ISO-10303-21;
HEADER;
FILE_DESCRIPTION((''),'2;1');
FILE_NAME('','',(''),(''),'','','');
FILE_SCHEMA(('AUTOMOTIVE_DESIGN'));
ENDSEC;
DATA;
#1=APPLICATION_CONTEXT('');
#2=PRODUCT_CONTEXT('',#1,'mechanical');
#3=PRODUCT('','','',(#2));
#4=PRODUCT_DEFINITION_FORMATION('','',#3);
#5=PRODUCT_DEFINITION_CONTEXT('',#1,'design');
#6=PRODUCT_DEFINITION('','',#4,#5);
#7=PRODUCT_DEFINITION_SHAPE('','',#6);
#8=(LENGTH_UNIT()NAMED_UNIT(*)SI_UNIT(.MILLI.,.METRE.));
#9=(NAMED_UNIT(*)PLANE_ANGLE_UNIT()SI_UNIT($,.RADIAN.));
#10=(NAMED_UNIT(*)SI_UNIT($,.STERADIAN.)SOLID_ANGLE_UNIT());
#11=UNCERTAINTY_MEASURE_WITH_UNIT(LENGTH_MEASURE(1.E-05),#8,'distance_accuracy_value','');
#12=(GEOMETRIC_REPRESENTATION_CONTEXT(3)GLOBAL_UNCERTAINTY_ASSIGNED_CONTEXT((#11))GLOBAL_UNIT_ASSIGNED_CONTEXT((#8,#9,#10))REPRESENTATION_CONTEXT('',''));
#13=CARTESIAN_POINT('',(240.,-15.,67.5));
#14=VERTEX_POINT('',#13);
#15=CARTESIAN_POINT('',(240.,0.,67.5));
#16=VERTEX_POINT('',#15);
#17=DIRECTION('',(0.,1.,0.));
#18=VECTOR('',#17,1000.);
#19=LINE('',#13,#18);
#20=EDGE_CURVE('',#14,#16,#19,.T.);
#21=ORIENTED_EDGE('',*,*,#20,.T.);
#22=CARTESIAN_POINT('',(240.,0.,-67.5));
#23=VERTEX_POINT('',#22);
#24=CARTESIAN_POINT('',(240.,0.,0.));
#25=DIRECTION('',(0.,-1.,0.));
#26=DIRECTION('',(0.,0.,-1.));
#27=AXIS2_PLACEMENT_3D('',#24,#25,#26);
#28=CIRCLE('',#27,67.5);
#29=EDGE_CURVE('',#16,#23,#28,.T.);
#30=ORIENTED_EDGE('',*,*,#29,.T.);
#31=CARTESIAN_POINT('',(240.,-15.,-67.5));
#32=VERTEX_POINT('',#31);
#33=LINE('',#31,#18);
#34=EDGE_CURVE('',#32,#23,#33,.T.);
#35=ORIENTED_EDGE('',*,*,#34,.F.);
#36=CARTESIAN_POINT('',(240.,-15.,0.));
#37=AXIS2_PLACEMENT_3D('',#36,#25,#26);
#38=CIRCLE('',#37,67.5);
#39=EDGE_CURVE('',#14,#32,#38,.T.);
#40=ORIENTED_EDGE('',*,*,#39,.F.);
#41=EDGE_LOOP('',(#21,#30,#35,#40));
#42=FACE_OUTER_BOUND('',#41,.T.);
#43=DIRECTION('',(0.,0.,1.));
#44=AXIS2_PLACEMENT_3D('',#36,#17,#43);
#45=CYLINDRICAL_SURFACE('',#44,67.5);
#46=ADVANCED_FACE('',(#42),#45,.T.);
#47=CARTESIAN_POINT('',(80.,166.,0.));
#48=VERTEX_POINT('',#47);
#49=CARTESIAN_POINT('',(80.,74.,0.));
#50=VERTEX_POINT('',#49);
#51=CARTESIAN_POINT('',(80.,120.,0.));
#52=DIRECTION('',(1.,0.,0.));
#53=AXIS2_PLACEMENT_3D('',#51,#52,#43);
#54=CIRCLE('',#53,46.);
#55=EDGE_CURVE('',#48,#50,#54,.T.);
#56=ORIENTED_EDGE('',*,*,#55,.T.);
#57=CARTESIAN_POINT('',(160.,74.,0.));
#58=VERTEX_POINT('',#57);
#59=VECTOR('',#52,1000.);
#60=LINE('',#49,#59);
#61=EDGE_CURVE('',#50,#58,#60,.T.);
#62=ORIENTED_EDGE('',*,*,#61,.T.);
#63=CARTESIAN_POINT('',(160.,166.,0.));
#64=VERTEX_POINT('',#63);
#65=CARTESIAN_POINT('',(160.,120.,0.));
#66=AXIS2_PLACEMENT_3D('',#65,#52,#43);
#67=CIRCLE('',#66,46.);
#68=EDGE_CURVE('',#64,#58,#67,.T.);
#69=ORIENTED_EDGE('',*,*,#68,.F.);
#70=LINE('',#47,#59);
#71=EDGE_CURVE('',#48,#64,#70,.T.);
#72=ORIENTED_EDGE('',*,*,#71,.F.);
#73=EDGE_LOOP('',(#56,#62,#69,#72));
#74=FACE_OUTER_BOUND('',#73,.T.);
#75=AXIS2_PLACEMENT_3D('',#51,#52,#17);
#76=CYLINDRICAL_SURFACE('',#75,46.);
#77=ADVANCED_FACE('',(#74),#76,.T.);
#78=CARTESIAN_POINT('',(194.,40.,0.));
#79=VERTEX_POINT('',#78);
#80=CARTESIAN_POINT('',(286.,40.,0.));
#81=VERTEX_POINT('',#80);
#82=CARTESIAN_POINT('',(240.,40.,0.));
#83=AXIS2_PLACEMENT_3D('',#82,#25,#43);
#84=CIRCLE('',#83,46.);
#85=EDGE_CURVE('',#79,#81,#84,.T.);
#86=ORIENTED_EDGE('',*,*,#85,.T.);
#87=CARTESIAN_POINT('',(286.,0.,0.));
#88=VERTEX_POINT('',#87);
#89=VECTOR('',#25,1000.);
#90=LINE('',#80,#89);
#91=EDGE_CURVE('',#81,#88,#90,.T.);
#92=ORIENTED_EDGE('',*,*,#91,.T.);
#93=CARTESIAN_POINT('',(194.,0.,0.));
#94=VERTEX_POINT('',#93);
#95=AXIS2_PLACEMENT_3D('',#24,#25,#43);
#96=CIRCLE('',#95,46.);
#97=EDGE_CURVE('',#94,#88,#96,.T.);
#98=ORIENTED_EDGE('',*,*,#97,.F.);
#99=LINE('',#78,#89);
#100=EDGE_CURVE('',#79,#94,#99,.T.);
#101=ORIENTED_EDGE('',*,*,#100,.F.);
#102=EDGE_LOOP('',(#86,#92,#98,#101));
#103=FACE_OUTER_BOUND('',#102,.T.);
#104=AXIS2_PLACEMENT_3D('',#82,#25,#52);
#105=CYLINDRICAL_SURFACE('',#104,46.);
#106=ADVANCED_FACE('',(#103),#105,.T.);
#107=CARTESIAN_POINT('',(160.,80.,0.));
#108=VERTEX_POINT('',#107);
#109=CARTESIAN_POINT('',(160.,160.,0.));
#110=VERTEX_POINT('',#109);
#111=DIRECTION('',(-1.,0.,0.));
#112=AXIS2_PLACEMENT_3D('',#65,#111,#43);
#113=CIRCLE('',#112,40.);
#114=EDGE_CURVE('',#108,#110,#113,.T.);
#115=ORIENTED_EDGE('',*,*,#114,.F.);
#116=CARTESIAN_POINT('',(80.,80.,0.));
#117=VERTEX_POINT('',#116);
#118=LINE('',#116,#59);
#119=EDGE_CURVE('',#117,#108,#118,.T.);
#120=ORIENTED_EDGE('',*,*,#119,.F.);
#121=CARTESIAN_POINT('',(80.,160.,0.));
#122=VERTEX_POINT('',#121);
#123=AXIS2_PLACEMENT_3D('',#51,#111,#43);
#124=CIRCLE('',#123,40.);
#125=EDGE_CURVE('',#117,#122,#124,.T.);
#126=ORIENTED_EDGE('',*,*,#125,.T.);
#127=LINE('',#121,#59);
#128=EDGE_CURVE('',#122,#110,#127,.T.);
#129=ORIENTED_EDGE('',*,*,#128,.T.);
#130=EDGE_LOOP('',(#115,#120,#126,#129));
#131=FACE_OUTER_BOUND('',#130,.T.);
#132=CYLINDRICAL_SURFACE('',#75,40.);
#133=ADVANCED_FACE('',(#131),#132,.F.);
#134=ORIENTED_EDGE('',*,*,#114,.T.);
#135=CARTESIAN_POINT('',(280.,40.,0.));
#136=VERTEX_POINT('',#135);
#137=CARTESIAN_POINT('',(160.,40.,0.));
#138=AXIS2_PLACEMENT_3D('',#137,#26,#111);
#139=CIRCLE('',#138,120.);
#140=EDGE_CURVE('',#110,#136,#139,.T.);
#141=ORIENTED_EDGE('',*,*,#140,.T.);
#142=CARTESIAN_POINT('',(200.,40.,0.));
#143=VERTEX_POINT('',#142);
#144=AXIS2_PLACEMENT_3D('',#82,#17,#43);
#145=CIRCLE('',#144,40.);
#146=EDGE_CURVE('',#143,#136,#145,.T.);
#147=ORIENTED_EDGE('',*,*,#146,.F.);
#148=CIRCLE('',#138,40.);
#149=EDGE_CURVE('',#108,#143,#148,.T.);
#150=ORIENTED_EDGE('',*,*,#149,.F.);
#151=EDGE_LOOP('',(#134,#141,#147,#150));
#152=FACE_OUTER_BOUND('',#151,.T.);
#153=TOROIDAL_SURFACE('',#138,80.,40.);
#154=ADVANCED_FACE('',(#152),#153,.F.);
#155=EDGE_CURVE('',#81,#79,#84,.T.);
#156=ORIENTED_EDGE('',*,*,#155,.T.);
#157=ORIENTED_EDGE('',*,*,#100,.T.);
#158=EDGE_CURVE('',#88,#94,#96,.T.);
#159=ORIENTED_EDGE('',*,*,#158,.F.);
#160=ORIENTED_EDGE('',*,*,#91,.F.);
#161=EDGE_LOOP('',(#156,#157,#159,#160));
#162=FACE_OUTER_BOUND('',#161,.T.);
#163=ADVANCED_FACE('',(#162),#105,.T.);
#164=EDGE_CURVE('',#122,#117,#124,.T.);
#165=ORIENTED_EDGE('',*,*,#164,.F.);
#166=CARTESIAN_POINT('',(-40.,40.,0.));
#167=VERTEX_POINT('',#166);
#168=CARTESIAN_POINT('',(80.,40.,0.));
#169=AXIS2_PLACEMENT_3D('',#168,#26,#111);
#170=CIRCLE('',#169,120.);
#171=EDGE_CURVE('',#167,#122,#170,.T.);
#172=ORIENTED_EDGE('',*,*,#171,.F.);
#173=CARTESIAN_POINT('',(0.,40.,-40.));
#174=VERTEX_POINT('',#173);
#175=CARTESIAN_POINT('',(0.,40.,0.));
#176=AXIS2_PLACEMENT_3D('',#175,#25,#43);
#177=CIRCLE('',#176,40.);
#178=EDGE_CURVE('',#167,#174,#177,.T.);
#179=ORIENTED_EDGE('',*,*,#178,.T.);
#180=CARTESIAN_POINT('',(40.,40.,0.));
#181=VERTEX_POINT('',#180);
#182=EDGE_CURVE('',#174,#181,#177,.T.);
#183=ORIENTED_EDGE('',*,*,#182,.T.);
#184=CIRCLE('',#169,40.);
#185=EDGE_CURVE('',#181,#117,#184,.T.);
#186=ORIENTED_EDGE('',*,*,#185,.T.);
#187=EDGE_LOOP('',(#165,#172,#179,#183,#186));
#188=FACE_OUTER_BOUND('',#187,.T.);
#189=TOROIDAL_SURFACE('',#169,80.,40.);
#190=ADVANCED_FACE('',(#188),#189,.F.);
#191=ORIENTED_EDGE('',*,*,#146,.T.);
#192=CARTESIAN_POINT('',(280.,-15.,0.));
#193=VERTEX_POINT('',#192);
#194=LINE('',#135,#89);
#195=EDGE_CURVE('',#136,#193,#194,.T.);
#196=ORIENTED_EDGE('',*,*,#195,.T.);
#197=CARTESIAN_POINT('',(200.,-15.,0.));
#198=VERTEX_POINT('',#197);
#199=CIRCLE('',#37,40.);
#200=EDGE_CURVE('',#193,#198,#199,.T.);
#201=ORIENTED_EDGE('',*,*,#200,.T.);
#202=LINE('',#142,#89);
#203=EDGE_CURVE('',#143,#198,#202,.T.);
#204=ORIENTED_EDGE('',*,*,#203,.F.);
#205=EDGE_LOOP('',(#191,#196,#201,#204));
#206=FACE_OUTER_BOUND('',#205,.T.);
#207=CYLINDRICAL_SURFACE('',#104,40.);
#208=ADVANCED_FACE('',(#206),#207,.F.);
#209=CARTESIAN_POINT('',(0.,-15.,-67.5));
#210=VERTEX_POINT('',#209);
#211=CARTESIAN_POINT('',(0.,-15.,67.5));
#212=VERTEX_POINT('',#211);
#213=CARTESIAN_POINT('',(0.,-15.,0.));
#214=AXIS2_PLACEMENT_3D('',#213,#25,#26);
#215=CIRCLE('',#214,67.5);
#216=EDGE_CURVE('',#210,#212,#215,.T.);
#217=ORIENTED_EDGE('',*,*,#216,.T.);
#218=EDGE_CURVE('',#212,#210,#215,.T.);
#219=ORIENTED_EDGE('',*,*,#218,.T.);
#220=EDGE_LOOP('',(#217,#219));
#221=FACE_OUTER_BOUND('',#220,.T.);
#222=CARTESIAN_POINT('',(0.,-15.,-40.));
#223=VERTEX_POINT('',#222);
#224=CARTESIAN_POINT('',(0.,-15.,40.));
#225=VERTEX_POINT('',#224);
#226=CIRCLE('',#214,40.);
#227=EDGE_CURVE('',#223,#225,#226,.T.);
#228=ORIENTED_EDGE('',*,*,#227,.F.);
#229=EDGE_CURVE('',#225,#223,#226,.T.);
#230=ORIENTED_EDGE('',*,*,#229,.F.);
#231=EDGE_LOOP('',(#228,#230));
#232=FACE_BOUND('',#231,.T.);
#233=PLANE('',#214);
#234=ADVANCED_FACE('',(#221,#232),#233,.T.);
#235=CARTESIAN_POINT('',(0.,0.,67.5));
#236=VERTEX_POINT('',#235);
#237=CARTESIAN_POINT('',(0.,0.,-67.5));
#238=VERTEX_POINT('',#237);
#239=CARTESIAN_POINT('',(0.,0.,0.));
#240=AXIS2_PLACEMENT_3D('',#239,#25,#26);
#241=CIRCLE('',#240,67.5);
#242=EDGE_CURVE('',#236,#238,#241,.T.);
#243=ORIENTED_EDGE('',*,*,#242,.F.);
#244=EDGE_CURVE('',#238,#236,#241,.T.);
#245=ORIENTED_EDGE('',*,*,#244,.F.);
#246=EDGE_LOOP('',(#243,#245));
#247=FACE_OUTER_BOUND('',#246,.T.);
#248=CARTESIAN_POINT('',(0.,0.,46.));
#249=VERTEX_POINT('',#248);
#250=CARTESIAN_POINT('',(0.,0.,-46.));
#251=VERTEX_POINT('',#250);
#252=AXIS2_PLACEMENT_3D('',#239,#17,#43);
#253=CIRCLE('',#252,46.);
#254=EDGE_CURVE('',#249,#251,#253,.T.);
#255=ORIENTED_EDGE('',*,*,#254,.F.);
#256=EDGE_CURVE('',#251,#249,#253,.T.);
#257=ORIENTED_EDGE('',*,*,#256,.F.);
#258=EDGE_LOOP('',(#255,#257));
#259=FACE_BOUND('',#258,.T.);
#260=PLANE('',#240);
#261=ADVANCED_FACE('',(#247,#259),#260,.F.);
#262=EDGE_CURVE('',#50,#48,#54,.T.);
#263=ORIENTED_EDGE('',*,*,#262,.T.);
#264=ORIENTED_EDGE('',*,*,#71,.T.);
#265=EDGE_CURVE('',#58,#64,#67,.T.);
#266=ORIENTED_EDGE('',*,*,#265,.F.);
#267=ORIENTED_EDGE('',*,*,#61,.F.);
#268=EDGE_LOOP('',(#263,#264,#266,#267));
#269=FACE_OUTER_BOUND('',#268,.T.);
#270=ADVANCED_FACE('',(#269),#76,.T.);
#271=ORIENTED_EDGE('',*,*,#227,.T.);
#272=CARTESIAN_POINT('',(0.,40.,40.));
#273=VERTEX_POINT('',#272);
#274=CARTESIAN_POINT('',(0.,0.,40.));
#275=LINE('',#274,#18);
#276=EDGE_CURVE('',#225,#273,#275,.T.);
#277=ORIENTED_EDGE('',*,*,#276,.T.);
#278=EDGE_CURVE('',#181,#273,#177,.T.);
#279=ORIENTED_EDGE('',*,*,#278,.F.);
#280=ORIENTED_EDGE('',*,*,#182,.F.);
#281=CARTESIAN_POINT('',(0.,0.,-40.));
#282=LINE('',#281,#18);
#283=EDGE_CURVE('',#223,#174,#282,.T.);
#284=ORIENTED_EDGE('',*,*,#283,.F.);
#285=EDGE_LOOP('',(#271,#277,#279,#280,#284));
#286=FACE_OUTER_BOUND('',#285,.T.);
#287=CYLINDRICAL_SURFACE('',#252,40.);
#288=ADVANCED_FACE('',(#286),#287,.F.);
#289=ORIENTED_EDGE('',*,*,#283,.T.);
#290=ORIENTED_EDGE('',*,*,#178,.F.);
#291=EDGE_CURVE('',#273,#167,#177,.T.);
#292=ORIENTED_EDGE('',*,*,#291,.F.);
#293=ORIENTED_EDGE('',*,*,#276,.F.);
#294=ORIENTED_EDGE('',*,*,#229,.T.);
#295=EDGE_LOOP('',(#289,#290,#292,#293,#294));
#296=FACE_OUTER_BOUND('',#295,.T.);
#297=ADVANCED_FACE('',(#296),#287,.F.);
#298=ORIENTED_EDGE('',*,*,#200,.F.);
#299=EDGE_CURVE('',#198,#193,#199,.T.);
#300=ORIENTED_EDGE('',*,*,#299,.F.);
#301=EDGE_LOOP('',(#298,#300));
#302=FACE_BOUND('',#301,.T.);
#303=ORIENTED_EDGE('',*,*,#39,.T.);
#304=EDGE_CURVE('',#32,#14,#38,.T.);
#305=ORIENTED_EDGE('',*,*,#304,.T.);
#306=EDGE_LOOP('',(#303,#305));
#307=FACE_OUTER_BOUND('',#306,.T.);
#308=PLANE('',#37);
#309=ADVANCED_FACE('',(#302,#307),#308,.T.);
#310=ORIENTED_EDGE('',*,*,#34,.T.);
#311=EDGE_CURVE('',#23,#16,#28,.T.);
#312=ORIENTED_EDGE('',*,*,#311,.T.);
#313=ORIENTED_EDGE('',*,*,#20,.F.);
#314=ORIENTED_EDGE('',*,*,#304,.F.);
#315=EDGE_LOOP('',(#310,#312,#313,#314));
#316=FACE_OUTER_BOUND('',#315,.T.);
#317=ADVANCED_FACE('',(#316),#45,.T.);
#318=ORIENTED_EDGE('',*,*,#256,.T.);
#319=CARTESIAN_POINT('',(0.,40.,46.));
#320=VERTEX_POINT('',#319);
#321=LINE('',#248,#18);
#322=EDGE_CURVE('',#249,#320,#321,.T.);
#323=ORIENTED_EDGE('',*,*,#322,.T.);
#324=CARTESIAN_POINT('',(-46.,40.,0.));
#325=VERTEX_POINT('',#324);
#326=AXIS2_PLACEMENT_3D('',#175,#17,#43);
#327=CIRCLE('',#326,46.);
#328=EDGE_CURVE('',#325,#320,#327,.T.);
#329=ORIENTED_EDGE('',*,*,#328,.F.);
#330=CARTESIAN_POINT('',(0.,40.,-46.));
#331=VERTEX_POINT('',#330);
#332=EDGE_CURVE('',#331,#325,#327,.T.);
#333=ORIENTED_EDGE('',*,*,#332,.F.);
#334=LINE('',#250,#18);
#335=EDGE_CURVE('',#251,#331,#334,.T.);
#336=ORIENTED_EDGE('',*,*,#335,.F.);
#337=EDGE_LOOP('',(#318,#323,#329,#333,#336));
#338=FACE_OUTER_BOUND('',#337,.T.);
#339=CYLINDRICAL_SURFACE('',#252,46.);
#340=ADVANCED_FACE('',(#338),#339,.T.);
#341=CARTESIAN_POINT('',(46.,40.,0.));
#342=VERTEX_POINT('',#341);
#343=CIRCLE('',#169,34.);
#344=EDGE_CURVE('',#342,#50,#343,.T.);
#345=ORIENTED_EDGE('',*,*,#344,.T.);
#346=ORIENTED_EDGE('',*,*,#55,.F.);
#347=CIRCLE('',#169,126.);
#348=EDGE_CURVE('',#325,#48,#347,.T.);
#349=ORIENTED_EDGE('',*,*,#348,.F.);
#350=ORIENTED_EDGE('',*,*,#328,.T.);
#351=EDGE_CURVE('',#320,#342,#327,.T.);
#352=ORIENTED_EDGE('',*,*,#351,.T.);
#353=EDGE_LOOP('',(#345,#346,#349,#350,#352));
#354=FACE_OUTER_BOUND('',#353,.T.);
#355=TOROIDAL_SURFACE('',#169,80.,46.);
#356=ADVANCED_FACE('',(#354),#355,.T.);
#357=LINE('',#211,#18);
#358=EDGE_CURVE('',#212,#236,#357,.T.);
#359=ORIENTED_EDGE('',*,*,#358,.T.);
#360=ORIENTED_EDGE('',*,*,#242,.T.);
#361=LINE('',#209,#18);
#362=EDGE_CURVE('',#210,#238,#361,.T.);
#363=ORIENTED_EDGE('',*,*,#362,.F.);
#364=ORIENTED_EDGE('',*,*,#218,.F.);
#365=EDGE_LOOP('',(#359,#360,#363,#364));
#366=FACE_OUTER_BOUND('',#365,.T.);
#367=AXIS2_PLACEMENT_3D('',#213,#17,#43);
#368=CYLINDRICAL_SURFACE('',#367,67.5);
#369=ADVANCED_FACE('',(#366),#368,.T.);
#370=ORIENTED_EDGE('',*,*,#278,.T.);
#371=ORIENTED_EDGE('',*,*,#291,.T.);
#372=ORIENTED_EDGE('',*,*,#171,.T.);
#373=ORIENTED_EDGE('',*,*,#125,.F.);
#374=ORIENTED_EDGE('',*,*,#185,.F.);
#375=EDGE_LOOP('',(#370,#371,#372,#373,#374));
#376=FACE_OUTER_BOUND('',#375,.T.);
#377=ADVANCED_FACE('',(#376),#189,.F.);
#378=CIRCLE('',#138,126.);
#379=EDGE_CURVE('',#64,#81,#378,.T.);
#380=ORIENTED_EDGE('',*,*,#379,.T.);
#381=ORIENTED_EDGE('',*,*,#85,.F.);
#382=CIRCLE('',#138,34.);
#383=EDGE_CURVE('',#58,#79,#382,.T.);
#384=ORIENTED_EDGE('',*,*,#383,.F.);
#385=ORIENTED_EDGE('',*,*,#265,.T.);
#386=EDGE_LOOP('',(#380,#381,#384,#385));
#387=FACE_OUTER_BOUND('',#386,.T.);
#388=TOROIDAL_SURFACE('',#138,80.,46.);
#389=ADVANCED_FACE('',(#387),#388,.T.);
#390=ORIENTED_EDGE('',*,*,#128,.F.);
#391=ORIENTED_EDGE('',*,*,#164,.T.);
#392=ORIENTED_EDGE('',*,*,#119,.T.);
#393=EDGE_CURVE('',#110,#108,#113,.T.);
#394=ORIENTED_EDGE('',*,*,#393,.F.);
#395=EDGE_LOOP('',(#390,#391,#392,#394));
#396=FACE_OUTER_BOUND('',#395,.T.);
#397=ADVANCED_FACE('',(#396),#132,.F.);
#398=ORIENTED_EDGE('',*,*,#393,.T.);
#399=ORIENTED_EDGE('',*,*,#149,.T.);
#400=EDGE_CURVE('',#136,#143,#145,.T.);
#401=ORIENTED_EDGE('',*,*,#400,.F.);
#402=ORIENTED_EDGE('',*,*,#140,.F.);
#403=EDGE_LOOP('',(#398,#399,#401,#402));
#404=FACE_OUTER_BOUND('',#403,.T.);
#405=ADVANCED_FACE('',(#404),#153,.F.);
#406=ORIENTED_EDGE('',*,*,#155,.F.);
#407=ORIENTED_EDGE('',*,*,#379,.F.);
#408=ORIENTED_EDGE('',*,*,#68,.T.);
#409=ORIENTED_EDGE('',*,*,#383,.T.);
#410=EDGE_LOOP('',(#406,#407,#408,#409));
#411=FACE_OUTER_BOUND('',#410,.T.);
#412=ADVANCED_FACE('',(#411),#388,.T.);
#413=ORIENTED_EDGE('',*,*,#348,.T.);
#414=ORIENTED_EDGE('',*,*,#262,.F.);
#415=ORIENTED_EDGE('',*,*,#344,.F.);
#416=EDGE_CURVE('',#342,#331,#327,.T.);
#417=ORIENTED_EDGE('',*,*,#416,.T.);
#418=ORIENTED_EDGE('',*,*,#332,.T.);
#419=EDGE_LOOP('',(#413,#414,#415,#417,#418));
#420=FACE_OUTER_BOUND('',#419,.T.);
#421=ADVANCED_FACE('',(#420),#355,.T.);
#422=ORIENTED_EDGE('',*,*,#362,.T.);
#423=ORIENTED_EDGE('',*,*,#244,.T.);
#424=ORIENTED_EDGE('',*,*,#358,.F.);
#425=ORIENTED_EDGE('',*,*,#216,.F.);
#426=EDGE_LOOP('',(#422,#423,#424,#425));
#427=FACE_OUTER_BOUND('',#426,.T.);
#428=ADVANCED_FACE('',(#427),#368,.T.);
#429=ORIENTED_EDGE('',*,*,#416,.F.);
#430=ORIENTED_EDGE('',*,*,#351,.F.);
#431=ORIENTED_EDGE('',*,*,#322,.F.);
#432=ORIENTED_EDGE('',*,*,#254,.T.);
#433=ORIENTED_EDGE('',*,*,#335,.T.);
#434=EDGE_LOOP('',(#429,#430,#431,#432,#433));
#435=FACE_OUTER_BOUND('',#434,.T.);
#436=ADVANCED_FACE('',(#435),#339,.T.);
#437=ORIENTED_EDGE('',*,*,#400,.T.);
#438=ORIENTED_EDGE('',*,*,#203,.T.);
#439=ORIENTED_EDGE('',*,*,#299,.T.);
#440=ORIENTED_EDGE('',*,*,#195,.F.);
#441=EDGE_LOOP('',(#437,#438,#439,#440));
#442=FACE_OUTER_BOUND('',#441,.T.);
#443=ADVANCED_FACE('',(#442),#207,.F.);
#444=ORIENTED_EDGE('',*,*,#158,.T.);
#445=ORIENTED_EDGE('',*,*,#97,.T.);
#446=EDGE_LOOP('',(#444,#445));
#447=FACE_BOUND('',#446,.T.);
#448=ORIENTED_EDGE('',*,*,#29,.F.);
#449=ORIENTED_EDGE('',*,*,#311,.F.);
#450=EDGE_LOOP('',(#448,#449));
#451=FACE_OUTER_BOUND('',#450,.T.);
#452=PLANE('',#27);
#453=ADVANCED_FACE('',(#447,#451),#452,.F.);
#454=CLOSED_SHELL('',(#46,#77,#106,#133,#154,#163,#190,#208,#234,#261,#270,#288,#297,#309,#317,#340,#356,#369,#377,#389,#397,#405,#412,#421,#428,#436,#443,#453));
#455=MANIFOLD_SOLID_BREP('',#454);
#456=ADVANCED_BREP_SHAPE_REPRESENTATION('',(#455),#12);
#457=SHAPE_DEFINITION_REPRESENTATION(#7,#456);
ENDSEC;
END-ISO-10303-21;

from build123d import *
from build123d.topology import SkipClean

# Parameters (mm, degrees)
SKETCH2_R           = 46
SKETCH2_R_2         = 40
SKETCH4_R           = 67.5
SKETCH4_R_2         = 40
BOSS_EXTRUDE1_DEPTH = 15


with BuildPart() as part:
    # Sweep1: sweep along a path in Sketch3
    with BuildLine(Plane.XY) as sweep1_path:
        Line((0, 0), (0, 40))
        ThreePointArc((0, 40), (23.431457505, 96.568542495), (80, 120))
        Line((80, 120), (160, 120))
        ThreePointArc((160, 120), (216.568542495, 96.568542495), (240, 40))
        Line((240, 40), (240, 0))
    # Sketch2 → Sweep1 (sweep)
    with BuildSketch(Plane(origin=(0, 0, 0), x_dir=(1, 0, 0), z_dir=(0, 1, 0))):
        Circle(SKETCH2_R)
        Circle(SKETCH2_R_2, mode=Mode.SUBTRACT)
    sweep(path=sweep1_path.line)

    # Sketch4 → Boss-Extrude1 (add)
    # profile 1 of 2: a face of its own
    with SkipClean():  # the faces are left unmerged after this step: merging them gives an invalid solid
        with BuildSketch(Plane(origin=(0, 0, 0), x_dir=(-1, 0, 0), z_dir=(0, -1, 0))):
            with Locations(Location((0, 0, 0), (0, 0, 90))):
                Circle(SKETCH4_R)
            Circle(SKETCH4_R_2, mode=Mode.SUBTRACT)
        # profile 2 of 2: a face of its own
        with BuildSketch(Plane(origin=(0, 0, 0), x_dir=(-1, 0, 0), z_dir=(0, -1, 0))):
            with Locations(Location((-240, 0, 0), (0, 0, 90))):
                Circle(SKETCH4_R)
            with Locations(Location((-240, 0, 0), (0, 0, 180))):
                Circle(SKETCH4_R_2, mode=Mode.SUBTRACT)
        extrude(amount=BOSS_EXTRUDE1_DEPTH)


solid = part.part
